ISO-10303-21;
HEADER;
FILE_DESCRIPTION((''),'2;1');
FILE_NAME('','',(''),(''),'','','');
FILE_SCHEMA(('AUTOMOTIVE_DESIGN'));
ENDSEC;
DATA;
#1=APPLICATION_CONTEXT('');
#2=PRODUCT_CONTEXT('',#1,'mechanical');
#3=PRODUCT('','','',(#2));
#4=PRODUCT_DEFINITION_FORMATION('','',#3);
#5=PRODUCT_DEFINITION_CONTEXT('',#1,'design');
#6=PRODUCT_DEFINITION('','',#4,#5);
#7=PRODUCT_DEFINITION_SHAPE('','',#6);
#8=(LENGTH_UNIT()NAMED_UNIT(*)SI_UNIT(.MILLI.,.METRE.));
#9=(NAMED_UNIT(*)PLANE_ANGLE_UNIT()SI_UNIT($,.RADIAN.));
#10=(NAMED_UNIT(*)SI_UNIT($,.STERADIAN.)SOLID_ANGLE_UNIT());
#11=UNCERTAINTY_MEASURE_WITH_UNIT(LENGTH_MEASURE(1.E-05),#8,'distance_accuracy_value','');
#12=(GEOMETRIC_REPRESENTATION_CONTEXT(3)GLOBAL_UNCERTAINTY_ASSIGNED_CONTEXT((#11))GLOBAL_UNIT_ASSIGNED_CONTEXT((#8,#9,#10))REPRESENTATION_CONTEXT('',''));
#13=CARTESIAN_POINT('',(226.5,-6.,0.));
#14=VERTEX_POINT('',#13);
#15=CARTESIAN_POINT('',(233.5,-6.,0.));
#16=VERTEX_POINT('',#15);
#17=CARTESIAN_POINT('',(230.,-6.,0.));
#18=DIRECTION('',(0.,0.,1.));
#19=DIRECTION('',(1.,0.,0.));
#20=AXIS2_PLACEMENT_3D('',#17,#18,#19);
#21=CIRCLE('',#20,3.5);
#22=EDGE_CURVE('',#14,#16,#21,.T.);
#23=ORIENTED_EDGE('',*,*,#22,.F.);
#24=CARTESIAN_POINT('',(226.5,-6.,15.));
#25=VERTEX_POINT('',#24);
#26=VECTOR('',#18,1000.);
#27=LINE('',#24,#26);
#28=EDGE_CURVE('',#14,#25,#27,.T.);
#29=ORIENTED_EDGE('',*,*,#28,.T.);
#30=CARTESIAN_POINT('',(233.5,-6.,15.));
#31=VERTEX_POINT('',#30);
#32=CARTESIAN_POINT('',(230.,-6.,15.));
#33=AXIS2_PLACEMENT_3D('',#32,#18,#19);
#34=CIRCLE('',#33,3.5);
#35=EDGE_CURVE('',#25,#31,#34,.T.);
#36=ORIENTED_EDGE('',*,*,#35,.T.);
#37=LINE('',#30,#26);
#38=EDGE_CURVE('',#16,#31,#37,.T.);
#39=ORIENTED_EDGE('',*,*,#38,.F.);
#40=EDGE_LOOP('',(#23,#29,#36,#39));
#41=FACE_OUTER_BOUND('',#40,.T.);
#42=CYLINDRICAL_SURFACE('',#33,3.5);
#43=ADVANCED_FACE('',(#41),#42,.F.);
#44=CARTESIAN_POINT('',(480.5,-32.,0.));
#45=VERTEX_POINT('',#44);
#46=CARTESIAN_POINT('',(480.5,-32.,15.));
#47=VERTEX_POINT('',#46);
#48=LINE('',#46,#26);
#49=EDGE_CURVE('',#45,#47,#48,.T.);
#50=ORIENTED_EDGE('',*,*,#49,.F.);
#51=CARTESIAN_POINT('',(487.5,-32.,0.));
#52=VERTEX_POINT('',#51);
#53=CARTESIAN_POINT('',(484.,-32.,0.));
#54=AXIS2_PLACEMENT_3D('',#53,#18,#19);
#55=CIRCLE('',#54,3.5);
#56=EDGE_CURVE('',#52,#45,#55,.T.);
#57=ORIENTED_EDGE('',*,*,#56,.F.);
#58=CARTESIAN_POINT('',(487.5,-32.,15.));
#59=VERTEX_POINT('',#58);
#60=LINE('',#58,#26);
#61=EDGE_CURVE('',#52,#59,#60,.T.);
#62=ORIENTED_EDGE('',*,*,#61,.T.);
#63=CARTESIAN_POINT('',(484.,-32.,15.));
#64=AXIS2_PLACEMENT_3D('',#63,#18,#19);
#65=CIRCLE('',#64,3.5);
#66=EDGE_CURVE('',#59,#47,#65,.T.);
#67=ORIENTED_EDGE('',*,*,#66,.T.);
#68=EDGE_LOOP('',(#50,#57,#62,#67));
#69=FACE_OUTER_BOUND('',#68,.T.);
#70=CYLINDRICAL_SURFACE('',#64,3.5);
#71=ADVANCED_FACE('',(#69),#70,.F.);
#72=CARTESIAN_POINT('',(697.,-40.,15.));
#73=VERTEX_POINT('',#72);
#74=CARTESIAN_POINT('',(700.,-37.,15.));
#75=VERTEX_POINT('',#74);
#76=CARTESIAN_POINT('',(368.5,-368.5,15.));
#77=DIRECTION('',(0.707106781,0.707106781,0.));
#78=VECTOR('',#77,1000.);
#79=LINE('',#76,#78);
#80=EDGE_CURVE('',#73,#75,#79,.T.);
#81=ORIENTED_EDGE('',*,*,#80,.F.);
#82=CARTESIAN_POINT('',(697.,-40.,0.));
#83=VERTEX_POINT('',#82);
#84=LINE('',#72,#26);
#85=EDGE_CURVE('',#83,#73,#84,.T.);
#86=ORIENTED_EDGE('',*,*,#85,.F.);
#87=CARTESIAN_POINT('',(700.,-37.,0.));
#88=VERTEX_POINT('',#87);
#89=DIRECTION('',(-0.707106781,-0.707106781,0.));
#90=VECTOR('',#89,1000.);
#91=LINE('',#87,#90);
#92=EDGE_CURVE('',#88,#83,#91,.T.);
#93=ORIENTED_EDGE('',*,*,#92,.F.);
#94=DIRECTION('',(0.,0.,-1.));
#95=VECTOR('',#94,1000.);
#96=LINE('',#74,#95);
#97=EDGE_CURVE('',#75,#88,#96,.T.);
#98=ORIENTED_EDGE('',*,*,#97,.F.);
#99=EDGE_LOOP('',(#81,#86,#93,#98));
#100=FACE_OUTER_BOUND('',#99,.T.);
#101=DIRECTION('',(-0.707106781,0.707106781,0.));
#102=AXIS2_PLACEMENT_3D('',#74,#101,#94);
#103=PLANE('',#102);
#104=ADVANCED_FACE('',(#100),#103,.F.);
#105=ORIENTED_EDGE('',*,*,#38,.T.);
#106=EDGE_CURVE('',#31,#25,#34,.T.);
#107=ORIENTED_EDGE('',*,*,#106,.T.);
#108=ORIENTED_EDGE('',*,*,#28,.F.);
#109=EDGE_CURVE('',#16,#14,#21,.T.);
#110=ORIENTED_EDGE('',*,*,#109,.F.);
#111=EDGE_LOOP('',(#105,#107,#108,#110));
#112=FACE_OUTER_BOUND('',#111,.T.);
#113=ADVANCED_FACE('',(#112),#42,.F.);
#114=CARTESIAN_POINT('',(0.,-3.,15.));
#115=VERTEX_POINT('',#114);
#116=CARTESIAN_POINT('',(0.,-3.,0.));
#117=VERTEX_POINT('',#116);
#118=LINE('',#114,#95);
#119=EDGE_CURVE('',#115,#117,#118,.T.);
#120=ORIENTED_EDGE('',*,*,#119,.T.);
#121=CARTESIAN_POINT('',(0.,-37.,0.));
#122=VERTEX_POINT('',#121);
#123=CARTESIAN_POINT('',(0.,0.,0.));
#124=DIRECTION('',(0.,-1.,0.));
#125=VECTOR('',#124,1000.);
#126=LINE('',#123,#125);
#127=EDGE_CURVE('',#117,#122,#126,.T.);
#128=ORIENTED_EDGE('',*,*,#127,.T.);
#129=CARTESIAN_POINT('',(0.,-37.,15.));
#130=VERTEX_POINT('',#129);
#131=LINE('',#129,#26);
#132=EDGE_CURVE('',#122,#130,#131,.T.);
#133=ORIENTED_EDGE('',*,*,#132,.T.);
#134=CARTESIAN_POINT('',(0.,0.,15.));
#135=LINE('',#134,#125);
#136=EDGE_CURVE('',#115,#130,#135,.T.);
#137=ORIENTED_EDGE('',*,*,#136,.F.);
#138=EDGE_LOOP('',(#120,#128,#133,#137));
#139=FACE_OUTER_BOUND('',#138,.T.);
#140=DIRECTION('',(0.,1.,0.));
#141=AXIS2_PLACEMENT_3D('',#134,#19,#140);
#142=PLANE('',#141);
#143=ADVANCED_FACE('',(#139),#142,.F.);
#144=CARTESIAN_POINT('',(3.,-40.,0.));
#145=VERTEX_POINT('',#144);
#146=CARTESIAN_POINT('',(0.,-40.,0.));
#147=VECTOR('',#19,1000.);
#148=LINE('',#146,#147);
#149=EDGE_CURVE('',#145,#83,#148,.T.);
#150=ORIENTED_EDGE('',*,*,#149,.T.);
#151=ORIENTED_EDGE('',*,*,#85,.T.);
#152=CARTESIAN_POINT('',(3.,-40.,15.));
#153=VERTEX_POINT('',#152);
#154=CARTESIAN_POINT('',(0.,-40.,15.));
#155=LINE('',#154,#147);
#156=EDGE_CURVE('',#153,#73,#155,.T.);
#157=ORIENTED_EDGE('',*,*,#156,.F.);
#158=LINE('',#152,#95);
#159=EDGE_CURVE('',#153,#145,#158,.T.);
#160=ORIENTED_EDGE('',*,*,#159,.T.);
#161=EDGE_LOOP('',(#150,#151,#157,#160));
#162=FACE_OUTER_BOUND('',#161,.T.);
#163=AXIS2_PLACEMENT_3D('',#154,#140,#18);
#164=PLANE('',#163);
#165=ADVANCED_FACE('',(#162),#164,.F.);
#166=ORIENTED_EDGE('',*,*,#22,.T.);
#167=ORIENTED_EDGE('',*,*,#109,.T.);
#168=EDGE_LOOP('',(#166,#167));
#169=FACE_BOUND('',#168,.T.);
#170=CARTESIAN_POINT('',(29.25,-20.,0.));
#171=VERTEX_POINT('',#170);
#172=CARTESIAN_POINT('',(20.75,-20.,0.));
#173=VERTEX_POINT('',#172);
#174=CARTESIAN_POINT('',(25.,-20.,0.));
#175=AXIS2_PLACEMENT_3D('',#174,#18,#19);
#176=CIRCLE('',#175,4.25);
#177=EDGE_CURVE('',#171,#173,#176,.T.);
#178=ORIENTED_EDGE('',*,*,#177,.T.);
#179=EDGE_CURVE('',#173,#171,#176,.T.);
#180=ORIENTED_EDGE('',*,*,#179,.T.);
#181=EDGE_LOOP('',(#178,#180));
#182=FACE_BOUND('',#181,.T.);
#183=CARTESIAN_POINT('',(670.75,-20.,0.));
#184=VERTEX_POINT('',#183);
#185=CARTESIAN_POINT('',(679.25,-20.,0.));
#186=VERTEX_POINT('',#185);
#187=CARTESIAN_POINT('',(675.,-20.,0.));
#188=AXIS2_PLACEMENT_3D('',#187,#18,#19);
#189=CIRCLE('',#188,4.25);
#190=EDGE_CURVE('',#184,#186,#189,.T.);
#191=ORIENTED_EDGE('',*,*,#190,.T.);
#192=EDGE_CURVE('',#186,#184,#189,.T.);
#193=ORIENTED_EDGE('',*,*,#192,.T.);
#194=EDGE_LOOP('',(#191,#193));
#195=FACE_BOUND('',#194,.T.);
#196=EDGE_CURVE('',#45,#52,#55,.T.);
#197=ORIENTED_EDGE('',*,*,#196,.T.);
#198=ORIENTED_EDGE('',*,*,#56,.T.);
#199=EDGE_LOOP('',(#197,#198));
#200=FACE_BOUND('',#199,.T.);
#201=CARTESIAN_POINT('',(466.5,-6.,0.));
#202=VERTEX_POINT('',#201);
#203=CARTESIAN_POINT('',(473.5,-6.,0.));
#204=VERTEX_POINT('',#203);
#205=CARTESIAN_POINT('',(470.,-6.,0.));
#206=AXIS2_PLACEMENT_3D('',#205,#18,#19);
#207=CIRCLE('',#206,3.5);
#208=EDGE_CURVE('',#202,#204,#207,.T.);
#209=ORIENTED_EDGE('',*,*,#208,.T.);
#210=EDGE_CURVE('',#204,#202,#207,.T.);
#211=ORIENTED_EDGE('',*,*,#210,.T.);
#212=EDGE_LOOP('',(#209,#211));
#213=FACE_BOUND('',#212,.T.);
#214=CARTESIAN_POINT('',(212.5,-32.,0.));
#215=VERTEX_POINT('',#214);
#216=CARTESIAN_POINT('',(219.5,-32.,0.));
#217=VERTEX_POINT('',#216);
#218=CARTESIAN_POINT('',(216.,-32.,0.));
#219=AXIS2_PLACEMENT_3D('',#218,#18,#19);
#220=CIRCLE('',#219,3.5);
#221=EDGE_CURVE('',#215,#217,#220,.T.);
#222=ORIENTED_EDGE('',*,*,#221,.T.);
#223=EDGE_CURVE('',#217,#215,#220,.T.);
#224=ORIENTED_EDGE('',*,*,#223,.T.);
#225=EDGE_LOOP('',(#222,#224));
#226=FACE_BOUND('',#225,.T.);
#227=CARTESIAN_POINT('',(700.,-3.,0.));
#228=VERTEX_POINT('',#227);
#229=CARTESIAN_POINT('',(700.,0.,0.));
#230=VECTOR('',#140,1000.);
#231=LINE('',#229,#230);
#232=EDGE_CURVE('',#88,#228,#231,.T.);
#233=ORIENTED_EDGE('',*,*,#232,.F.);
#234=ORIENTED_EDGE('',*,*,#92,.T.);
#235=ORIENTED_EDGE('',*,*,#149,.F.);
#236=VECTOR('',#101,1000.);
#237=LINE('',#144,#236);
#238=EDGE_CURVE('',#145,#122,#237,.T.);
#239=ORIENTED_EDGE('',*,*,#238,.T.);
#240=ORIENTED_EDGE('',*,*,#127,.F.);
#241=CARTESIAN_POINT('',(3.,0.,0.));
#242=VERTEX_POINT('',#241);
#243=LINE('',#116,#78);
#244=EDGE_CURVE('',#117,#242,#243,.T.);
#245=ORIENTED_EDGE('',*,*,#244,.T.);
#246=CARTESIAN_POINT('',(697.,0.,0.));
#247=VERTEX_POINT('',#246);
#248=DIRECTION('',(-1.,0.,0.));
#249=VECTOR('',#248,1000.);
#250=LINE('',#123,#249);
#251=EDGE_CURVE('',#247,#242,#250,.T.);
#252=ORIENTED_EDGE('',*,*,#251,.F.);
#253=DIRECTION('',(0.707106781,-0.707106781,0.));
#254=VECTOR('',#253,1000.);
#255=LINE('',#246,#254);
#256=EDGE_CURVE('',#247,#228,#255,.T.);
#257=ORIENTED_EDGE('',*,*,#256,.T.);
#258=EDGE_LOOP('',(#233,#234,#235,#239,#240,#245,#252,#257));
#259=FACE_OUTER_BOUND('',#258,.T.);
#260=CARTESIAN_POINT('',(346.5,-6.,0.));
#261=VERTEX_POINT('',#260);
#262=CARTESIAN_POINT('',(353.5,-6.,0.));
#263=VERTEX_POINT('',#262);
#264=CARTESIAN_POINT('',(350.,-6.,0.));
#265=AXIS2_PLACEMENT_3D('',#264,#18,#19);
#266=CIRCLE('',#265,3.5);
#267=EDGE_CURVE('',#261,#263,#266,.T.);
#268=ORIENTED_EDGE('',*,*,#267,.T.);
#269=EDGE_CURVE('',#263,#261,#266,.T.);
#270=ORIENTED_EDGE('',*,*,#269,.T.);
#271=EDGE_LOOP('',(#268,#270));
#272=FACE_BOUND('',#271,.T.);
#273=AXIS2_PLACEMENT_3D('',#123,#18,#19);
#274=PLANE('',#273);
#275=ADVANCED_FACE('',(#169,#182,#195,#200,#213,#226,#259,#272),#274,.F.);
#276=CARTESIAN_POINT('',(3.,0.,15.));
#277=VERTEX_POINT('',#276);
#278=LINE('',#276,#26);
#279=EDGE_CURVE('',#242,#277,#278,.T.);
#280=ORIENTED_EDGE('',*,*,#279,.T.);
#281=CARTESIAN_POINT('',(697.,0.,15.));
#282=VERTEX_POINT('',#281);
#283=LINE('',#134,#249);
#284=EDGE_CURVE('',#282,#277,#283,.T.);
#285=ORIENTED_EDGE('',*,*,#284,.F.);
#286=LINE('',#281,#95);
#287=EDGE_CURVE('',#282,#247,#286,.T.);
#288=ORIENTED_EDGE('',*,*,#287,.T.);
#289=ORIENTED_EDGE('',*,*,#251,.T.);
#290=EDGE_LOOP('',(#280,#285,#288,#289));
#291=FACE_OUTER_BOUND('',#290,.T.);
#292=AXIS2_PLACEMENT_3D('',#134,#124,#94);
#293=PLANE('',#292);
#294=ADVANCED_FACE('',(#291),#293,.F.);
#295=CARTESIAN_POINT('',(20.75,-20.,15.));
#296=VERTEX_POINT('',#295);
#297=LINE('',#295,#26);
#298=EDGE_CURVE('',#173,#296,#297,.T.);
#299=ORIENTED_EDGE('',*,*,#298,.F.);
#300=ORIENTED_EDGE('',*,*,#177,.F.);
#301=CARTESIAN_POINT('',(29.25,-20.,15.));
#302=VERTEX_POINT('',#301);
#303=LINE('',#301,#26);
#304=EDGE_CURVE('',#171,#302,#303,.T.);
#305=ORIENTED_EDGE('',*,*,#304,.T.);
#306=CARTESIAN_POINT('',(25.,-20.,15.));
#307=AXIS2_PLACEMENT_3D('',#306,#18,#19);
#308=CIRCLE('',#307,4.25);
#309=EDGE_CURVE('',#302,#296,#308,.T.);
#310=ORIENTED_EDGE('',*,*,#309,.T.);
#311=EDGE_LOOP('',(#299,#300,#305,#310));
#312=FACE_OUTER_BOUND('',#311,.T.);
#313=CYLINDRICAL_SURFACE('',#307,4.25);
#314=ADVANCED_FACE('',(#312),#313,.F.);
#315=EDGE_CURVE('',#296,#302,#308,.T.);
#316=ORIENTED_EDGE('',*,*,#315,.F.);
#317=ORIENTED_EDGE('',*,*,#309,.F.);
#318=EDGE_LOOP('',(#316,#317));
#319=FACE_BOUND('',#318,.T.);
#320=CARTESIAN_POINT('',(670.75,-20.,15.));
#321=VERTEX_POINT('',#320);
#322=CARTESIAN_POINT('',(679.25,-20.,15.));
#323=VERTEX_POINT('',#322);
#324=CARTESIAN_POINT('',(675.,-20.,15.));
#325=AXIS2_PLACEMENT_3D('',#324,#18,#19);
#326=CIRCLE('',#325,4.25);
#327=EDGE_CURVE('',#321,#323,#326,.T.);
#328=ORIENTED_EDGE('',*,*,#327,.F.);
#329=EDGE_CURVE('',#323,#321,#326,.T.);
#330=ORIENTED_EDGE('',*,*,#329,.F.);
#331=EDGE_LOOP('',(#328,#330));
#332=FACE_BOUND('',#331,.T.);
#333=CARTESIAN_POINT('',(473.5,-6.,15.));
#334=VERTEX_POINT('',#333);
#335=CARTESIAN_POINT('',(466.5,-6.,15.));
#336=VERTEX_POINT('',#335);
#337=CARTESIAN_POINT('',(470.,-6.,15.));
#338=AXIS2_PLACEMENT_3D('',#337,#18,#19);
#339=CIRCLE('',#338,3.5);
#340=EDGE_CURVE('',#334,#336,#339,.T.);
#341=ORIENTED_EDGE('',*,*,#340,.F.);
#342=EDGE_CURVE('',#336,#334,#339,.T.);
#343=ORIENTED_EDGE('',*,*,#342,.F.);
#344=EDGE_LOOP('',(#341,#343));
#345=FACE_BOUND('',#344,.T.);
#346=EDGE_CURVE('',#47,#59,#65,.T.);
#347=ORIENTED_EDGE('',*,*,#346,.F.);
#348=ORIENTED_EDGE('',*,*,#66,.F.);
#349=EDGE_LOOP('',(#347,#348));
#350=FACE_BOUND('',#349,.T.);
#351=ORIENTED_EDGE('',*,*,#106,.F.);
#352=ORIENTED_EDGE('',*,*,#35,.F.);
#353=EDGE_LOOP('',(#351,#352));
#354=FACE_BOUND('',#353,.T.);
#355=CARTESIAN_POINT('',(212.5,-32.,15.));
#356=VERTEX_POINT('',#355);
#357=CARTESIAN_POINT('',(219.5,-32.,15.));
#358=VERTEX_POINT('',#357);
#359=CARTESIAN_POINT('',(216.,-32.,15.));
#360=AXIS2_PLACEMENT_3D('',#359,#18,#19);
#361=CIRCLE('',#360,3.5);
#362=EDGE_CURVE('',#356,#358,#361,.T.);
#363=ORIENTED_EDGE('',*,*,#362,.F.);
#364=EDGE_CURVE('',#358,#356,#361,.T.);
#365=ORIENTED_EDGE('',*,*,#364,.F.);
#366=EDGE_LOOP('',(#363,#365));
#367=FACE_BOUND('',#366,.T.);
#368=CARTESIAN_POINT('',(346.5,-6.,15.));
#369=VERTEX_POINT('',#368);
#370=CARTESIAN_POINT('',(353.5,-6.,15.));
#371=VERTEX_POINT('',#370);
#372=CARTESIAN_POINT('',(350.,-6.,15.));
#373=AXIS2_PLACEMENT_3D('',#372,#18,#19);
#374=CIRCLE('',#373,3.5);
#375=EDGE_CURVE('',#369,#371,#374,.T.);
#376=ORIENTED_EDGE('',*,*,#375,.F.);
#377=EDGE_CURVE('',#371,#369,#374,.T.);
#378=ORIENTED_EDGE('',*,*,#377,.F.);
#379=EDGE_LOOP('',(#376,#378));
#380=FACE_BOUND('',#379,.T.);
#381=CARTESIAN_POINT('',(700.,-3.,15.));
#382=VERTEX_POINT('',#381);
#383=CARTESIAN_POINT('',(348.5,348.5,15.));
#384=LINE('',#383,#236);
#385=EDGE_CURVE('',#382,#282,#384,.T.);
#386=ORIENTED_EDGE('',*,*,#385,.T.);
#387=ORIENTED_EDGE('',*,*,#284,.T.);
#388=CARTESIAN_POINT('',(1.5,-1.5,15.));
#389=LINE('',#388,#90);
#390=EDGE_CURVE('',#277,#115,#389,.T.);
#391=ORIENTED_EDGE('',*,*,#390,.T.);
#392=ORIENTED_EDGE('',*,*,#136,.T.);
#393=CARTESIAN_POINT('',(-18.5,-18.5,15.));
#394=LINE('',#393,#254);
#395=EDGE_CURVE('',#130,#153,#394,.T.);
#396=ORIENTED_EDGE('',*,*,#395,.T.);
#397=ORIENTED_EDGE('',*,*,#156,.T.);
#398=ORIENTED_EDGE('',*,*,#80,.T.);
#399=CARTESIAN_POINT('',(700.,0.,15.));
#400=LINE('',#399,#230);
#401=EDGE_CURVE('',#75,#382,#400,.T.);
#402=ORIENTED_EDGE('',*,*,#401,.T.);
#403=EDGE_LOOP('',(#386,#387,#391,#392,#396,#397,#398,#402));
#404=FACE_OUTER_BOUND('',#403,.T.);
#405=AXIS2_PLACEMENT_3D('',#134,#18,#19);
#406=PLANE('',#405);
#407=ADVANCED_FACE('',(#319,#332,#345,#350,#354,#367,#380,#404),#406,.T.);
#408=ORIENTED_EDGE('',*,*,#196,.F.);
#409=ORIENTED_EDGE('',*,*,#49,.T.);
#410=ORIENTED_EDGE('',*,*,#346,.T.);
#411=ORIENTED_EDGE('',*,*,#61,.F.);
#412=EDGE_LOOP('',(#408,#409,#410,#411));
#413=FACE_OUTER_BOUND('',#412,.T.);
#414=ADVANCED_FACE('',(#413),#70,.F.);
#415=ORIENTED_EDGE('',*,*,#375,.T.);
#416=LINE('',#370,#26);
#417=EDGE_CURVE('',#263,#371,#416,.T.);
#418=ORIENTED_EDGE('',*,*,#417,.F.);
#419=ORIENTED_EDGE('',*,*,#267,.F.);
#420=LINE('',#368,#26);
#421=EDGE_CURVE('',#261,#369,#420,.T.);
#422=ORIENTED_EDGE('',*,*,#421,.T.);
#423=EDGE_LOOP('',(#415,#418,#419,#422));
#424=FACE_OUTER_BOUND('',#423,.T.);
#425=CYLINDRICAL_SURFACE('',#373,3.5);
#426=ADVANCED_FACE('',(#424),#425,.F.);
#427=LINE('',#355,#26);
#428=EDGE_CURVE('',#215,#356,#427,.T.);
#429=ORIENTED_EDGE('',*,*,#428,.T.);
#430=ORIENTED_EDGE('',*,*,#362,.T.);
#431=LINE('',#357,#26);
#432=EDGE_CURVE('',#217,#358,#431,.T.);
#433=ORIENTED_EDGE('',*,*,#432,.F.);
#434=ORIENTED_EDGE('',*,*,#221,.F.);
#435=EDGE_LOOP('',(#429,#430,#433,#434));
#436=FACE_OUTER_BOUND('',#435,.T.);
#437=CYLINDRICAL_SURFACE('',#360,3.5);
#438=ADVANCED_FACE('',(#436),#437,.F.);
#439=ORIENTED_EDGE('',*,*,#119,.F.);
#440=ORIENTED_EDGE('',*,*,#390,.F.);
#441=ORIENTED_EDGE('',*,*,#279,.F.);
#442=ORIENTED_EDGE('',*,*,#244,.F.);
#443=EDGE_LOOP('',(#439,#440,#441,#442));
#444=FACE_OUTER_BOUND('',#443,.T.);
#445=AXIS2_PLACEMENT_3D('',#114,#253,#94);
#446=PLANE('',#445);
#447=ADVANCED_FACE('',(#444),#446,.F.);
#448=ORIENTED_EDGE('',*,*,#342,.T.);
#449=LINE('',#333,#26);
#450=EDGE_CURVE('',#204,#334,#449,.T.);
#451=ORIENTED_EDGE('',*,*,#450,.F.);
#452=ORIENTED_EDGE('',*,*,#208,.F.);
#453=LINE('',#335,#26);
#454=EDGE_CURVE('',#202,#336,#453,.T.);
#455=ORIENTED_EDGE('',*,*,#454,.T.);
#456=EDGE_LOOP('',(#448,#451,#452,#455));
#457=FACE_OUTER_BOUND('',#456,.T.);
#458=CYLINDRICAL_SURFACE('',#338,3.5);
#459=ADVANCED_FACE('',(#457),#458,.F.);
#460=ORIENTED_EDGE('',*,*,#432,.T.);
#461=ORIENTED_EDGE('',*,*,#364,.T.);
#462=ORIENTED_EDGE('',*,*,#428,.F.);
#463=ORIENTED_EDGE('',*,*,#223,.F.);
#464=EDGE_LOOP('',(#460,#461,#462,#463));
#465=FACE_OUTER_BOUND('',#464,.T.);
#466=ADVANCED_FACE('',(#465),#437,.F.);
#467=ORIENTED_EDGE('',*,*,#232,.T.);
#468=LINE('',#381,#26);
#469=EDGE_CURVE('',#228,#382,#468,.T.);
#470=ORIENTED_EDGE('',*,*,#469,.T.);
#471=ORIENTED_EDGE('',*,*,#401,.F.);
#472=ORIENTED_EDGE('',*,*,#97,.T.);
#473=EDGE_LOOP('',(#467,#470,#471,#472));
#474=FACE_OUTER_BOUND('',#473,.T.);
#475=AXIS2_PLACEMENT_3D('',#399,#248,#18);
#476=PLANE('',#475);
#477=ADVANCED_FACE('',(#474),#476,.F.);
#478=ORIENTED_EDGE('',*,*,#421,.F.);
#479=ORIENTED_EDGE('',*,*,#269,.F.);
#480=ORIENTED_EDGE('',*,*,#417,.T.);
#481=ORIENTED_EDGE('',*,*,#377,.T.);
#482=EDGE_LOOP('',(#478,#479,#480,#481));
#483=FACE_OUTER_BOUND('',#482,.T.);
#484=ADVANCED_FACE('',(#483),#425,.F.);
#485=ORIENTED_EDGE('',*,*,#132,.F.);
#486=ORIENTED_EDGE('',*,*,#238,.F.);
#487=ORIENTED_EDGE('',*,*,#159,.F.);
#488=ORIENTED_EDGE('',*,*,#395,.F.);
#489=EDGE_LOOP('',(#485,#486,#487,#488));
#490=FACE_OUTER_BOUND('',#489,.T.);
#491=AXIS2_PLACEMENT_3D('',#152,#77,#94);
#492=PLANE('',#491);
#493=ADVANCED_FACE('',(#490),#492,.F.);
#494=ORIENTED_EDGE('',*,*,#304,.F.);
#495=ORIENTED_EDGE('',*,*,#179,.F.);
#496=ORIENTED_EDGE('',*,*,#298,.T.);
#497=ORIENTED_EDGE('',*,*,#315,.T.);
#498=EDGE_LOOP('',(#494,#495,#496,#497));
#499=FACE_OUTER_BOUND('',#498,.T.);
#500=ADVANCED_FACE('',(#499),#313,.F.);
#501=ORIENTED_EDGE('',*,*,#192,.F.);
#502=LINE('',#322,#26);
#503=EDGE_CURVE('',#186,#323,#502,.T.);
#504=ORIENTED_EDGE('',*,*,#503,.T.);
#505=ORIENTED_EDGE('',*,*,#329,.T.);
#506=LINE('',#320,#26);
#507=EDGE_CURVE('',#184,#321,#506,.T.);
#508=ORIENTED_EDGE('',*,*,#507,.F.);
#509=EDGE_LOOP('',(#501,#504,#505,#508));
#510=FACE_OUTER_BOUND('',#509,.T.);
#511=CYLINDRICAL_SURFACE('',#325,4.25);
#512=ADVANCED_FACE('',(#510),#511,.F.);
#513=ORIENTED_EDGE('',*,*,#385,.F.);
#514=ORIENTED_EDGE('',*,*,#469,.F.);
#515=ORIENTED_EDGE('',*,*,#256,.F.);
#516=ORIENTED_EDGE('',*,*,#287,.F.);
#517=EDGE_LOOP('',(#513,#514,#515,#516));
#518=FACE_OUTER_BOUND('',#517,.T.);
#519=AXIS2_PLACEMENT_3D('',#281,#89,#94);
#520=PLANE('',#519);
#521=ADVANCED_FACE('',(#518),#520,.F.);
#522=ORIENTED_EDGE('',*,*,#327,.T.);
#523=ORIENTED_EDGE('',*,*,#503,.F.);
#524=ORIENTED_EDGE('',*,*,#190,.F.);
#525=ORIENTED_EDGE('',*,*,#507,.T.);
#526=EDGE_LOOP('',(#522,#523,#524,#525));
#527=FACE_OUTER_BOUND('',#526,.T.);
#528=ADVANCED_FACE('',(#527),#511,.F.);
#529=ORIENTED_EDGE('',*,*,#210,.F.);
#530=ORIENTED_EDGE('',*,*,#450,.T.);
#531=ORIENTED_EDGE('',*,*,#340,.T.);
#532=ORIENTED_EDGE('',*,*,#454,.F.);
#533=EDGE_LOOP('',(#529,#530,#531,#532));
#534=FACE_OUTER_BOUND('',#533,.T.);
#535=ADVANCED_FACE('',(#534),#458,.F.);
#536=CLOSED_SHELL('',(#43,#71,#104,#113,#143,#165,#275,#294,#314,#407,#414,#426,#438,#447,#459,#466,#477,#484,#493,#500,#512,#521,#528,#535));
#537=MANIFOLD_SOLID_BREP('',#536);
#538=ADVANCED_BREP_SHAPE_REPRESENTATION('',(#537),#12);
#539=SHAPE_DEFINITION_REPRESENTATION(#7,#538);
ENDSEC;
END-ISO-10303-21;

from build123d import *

# Parameters (mm, degrees)
SKETCH_1_W            = 700
SKETCH_1_H            = 40
EXTRUDE_1_DEPTH       = 15
CHAMFER_1_SIZE        = 3
HOLE_WIZARD_M10_1_D   = 8.5
HOLE_WIZARD_7_0_7_1_D = 7


with BuildPart() as part:
    # 草图1 → 凸台-拉伸1 (new body)
    with BuildSketch(Plane.XY):
        with Locations((350, -20)):
            Rectangle(SKETCH_1_W, SKETCH_1_H)
    extrude(amount=EXTRUDE_1_DEPTH)

    # 倒角1
    chamfer_1_edges = [part.edges().sort_by_distance(p)[0] for p in [
        (0, 0, 7.5),
        (700, 0, 7.5),
        (700, -40, 7.5),
        (0, -40, 7.5),
    ]]
    chamfer(chamfer_1_edges, length=CHAMFER_1_SIZE)

    # M10 螺纹孔1 (through all)
    with Locations(Plane.XY.offset(15)):
        with Locations((25, -20), (675, -20)):
            Hole(HOLE_WIZARD_M10_1_D / 2)

    # Ø7.0 (7) 直径孔1 (through all)
    with Locations(Plane.XY.offset(15)):
        with Locations((470, -6), (350, -6), (230, -6), (216, -32), (484, -32)):
            Hole(HOLE_WIZARD_7_0_7_1_D / 2)


solid = part.part
